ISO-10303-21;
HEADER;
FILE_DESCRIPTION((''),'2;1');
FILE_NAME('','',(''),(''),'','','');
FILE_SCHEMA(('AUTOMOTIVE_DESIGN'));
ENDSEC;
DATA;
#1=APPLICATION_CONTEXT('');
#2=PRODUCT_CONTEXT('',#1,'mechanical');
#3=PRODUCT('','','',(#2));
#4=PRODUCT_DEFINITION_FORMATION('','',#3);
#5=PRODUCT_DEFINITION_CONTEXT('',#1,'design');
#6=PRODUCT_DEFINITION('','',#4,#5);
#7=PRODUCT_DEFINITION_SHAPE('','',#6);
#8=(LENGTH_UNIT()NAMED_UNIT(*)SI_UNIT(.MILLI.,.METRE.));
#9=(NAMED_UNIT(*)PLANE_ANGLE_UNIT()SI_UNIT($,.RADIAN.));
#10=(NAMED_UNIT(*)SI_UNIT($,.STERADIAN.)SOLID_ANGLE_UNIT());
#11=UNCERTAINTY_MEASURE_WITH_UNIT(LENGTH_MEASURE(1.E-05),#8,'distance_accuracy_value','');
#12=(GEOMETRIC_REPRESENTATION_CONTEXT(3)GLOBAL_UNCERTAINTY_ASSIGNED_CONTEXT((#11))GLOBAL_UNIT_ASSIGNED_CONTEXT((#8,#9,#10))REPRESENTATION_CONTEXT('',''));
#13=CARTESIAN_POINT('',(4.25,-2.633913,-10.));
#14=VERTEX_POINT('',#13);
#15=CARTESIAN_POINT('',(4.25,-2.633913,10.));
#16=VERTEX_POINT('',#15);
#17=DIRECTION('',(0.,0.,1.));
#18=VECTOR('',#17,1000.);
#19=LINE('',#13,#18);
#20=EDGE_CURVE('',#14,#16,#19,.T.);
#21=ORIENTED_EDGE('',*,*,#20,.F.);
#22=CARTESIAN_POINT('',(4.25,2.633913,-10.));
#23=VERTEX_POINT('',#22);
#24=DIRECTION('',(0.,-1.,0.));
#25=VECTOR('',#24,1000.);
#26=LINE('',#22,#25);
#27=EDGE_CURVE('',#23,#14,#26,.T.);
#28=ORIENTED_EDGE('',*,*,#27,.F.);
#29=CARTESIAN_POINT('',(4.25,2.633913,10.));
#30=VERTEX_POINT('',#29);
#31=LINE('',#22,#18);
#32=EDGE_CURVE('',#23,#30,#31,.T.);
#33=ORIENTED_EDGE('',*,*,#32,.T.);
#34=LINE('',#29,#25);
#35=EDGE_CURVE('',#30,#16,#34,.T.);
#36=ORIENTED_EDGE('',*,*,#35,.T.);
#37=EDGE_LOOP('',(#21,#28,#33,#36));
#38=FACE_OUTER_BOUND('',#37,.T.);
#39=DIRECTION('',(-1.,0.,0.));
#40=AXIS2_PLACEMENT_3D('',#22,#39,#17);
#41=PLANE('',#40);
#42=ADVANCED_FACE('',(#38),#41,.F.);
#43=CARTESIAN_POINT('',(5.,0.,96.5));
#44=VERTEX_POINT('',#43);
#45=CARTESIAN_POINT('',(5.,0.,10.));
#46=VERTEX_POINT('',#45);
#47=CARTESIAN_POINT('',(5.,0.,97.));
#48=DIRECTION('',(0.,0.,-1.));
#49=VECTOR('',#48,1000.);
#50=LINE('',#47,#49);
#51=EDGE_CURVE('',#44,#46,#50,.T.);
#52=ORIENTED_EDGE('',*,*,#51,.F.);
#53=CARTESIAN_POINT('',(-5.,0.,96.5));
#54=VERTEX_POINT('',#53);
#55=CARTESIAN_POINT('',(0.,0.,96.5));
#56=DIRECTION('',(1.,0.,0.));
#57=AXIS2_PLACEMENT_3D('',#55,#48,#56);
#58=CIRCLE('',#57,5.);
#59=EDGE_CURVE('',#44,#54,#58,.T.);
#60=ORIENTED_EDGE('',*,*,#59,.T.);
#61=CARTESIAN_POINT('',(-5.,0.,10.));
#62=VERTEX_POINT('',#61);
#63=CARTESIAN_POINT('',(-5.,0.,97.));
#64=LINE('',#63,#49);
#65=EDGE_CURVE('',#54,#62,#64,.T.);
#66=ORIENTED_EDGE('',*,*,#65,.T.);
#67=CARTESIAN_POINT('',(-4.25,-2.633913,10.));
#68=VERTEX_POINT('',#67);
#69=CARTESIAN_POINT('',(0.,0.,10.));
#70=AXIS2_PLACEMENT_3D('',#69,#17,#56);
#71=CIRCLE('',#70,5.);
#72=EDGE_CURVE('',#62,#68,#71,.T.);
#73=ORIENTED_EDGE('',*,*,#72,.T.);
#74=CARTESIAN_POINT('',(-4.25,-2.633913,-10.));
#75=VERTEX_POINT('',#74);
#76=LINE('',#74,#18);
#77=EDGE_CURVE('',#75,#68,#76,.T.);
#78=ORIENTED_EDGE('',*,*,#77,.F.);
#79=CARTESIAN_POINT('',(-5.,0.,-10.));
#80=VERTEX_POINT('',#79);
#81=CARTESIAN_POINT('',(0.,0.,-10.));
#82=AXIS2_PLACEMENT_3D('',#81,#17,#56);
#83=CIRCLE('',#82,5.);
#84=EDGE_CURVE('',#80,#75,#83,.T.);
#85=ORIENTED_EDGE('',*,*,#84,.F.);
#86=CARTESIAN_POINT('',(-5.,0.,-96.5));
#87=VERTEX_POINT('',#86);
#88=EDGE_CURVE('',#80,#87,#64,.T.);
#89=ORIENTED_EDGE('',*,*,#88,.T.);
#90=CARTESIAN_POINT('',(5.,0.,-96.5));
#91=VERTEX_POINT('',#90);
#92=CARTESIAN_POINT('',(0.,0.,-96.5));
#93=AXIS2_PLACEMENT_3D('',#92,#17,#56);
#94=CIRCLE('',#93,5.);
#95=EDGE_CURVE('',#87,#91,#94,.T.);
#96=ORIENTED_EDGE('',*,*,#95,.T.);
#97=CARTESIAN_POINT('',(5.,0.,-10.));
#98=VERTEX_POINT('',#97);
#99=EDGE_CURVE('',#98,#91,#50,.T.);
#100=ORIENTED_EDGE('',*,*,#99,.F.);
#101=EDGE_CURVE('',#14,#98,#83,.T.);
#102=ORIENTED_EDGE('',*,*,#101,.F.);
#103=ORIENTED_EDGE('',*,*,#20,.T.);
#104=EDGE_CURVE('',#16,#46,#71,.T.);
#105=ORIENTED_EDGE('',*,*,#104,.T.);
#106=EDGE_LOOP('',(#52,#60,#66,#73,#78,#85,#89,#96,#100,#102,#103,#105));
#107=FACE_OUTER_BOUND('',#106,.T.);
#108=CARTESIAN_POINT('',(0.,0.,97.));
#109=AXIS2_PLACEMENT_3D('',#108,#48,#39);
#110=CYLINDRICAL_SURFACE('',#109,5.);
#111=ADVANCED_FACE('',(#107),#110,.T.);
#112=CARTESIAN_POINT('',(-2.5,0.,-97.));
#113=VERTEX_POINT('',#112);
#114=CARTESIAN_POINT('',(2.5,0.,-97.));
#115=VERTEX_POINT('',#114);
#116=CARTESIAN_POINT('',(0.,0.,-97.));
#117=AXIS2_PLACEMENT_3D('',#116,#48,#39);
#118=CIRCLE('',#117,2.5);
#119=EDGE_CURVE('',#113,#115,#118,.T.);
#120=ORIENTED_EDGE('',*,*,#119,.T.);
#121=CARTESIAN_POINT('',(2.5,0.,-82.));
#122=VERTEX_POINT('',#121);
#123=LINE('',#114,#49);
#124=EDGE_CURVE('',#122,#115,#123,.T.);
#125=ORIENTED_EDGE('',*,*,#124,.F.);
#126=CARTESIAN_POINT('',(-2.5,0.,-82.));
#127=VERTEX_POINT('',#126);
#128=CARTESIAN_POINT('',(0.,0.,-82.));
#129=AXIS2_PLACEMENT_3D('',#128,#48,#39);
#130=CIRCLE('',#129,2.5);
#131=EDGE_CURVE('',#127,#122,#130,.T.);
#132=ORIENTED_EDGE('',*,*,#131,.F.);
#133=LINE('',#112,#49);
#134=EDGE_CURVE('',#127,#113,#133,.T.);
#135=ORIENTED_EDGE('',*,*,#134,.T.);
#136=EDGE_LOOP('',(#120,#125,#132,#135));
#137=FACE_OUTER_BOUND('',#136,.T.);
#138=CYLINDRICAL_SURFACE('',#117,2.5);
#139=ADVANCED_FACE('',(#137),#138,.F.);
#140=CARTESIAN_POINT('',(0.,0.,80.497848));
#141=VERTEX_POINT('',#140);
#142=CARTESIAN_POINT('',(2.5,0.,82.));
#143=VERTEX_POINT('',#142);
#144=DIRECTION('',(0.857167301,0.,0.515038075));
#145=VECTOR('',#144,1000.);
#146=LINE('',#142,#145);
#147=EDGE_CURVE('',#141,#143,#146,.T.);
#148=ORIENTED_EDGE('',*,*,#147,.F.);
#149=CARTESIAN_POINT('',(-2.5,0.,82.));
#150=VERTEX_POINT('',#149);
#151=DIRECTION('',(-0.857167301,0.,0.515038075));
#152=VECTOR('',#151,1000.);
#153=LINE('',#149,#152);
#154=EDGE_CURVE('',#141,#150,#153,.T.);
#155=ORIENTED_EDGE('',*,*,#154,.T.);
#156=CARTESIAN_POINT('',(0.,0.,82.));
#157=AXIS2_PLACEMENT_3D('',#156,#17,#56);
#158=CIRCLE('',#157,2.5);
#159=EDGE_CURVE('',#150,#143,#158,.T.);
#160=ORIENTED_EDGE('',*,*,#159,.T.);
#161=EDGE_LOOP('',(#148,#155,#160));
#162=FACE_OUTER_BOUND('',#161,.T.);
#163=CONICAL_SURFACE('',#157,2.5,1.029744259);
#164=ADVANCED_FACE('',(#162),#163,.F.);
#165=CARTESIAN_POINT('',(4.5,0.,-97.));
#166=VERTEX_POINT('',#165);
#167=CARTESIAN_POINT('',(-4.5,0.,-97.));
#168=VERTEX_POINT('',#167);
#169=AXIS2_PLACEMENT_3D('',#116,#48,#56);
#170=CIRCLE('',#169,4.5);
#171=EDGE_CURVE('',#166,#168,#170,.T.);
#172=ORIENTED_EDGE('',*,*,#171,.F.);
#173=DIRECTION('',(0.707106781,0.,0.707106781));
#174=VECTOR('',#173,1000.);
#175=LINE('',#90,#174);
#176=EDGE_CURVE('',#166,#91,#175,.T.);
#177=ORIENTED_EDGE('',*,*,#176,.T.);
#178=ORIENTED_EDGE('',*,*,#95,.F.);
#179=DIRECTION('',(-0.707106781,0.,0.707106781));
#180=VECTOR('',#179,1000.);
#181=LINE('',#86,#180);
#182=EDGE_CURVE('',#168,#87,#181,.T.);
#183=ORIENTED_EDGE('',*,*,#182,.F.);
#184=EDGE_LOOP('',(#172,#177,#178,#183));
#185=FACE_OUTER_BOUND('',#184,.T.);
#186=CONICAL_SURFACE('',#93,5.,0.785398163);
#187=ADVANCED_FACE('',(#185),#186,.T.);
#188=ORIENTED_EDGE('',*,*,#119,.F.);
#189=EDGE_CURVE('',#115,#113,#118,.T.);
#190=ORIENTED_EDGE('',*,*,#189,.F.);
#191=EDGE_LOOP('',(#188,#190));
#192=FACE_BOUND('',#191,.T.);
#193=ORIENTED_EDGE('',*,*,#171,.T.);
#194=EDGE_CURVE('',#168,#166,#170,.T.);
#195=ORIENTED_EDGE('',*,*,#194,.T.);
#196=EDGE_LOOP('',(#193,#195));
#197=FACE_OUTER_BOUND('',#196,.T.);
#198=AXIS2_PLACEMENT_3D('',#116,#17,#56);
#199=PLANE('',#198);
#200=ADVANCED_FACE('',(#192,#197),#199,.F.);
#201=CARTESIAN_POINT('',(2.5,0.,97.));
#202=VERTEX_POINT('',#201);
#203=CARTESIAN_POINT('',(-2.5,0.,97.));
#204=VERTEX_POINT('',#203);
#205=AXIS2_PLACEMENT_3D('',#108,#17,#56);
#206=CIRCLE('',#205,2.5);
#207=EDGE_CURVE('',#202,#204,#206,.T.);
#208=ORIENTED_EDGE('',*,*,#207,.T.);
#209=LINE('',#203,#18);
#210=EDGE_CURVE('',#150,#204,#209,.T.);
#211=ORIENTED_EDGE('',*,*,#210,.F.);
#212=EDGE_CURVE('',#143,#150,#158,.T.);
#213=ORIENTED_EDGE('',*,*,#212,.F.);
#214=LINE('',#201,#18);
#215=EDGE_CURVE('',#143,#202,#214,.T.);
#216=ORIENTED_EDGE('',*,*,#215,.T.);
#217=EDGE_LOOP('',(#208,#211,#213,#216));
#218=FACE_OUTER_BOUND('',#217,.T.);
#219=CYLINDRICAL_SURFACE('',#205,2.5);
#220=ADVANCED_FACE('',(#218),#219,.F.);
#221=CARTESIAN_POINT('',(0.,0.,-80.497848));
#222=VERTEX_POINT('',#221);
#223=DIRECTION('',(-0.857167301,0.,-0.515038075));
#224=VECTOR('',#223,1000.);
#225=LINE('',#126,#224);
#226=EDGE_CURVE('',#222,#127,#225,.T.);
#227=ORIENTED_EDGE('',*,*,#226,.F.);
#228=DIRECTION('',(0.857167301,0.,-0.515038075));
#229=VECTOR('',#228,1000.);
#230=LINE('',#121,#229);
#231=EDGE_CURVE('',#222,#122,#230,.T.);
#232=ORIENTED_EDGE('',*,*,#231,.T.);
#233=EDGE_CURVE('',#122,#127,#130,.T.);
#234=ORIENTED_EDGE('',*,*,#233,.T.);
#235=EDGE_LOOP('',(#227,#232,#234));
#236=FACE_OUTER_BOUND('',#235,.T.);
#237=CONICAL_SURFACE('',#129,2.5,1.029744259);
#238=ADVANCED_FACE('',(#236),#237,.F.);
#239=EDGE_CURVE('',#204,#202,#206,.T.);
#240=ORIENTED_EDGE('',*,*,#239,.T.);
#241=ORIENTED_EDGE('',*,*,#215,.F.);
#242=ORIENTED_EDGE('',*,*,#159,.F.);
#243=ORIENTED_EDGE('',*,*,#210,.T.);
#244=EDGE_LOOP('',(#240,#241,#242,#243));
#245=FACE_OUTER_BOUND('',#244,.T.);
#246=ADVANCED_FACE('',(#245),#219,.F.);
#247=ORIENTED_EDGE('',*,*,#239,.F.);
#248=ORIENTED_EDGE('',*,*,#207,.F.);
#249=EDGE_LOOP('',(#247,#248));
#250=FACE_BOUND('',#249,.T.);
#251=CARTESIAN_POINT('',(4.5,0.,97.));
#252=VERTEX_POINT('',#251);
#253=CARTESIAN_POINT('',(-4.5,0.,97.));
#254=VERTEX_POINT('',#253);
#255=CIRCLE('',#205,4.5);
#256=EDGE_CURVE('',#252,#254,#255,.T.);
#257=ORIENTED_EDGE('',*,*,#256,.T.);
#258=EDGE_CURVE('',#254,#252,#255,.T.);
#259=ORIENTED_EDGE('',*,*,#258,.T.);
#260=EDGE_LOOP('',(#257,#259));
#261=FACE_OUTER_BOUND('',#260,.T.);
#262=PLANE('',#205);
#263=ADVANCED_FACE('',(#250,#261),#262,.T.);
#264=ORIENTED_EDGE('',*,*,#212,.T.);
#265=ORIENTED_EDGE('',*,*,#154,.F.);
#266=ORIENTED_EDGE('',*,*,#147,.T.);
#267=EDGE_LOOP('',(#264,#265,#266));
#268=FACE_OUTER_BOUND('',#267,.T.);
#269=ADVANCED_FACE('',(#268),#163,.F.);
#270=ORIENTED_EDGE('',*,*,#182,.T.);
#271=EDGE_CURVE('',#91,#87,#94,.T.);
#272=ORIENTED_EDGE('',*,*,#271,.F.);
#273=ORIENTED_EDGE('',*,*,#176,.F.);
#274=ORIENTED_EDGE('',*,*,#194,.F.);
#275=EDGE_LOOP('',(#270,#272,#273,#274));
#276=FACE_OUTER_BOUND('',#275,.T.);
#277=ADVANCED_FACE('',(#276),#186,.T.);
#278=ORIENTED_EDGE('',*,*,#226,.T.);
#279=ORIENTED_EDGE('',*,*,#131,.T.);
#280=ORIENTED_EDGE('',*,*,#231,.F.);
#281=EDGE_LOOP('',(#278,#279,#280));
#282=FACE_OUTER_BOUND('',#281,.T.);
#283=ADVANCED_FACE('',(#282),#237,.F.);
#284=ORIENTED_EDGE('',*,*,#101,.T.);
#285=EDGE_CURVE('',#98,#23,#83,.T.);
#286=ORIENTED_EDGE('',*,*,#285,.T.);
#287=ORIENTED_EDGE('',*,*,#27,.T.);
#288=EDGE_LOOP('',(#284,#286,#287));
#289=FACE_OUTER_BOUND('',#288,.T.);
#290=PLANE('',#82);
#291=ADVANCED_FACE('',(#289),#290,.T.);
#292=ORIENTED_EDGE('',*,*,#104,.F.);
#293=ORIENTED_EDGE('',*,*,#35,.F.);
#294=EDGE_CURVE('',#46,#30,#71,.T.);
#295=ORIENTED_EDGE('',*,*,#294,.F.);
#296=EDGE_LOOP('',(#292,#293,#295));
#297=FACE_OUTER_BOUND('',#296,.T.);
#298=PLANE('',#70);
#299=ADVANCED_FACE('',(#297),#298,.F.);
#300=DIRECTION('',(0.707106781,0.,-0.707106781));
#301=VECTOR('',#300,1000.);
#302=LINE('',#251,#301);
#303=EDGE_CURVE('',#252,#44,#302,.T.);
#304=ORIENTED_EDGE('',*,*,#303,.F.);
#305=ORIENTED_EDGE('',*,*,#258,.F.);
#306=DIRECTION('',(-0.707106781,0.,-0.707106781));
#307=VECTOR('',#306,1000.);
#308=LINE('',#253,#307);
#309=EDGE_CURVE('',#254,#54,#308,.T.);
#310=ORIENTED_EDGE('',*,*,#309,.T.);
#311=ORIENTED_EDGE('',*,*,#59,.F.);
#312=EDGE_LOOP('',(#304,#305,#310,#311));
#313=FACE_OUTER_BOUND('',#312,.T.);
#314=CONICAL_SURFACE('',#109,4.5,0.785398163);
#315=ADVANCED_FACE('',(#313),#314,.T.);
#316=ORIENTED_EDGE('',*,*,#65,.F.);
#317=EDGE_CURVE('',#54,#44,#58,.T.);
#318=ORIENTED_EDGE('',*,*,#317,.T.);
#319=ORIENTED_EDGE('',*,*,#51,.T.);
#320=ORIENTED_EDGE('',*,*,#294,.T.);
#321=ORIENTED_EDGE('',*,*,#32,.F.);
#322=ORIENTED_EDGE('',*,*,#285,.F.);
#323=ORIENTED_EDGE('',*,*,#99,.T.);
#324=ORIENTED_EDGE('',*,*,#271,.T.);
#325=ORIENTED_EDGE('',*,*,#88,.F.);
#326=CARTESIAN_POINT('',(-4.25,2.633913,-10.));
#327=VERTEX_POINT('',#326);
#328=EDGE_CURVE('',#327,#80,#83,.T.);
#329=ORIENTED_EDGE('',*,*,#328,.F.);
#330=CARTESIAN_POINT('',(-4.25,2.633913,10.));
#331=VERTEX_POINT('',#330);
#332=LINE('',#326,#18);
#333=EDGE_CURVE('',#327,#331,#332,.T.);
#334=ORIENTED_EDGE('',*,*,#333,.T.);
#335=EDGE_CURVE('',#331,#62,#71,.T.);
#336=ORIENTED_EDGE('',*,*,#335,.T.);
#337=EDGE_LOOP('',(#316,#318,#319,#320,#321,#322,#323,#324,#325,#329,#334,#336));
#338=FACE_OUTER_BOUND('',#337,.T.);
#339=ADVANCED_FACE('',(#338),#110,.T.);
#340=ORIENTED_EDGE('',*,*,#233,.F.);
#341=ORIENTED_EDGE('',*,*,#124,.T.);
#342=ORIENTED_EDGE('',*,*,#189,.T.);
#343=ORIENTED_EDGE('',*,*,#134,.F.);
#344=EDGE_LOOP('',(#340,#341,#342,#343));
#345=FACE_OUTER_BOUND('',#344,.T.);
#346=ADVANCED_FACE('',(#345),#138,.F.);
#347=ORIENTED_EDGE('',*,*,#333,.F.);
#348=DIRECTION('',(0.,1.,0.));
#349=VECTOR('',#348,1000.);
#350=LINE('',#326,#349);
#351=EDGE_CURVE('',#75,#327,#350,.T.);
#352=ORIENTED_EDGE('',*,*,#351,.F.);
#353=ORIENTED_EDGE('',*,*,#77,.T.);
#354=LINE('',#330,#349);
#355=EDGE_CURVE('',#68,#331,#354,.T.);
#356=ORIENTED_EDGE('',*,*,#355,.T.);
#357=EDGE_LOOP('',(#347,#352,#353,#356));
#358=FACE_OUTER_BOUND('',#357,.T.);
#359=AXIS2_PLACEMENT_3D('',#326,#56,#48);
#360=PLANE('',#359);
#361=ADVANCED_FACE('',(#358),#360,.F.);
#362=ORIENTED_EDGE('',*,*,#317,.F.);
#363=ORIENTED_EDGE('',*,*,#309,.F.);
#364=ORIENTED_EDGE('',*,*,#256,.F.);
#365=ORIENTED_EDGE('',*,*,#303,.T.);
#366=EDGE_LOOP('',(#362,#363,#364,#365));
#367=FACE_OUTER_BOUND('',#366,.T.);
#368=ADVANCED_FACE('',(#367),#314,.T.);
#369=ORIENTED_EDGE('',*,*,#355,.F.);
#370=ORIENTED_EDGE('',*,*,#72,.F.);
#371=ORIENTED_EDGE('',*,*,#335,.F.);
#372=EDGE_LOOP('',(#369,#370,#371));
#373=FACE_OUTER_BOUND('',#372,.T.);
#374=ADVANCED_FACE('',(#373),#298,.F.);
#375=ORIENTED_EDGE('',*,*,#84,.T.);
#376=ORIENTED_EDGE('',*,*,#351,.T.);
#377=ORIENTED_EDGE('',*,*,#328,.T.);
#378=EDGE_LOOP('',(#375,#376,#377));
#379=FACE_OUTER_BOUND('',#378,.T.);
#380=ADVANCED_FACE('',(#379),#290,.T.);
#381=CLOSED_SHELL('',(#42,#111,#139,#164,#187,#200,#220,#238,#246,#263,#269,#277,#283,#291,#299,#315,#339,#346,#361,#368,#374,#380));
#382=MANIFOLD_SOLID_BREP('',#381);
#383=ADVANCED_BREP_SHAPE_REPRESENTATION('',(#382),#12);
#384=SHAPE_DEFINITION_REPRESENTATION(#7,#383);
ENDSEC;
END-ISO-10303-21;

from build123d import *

# Parameters (mm, degrees)
SKETCH_1_R             = 5
EXTRUDE_1_DEPTH        = 97
CUT_EXTRUDE_1_DEPTH    = 10
HOLE_WIZARD_M6_1_D     = 5
HOLE_WIZARD_M6_1_DEPTH = 15
HOLE_WIZARD_M6_1_TIP   = 1.502151548
HOLE_WIZARD_M6_2_D     = 5
HOLE_WIZARD_M6_2_DEPTH = 15
HOLE_WIZARD_M6_2_TIP   = 1.502151548
CHAMFER_1_SIZE         = 0.5


with BuildPart() as part:
    # 草图1 → 凸台-拉伸1 (new, symmetric)
    with BuildSketch(Plane.XY):
        with Locations(Location((0, 0, 0), (0, 0, 180))):
            Circle(SKETCH_1_R)
    extrude(amount=EXTRUDE_1_DEPTH, both=True)

    # 草图2 → 切除-拉伸1 (cut, symmetric)
    with BuildSketch(Plane.XY):
        with BuildLine():
            Line((-4.25, 2.633913438), (-4.25, -2.633913438))
            ThreePointArc((-4.25, -2.633913438), (-5, 0), (-4.25, 2.633913438))
        make_face()
        with BuildLine():
            Line((4.25, 2.633913438), (4.25, -2.633913438))
            ThreePointArc((4.25, -2.633913438), (5, 0), (4.25, 2.633913438))
        make_face()
    extrude(amount=CUT_EXTRUDE_1_DEPTH, both=True, mode=Mode.SUBTRACT)

    # M6 螺纹孔1
    with Locations(Plane.XY.offset(97)):
        with Locations((0, 0)):
            Hole(HOLE_WIZARD_M6_1_D / 2, depth=HOLE_WIZARD_M6_1_DEPTH)
            with Locations((0, 0, -(HOLE_WIZARD_M6_1_DEPTH + HOLE_WIZARD_M6_1_TIP / 2))):  # 118° drill point
                Cone(0, HOLE_WIZARD_M6_1_D / 2, HOLE_WIZARD_M6_1_TIP, mode=Mode.SUBTRACT)

    # M6 螺纹孔2
    with Locations(Plane(origin=(0, 0, -97), x_dir=(-1, 0, 0), z_dir=(0, 0, -1))):
        with Locations((0, 0)):
            Hole(HOLE_WIZARD_M6_2_D / 2, depth=HOLE_WIZARD_M6_2_DEPTH)
            with Locations((0, 0, -(HOLE_WIZARD_M6_2_DEPTH + HOLE_WIZARD_M6_2_TIP / 2))):  # 118° drill point
                Cone(0, HOLE_WIZARD_M6_2_D / 2, HOLE_WIZARD_M6_2_TIP, mode=Mode.SUBTRACT)

    # 倒角1
    chamfer_1_edges = [part.edges().sort_by_distance(p)[0] for p in [
        (5, 0, -97),
        (5, 0, 97),
    ]]
    chamfer(chamfer_1_edges, length=CHAMFER_1_SIZE)


solid = part.part
